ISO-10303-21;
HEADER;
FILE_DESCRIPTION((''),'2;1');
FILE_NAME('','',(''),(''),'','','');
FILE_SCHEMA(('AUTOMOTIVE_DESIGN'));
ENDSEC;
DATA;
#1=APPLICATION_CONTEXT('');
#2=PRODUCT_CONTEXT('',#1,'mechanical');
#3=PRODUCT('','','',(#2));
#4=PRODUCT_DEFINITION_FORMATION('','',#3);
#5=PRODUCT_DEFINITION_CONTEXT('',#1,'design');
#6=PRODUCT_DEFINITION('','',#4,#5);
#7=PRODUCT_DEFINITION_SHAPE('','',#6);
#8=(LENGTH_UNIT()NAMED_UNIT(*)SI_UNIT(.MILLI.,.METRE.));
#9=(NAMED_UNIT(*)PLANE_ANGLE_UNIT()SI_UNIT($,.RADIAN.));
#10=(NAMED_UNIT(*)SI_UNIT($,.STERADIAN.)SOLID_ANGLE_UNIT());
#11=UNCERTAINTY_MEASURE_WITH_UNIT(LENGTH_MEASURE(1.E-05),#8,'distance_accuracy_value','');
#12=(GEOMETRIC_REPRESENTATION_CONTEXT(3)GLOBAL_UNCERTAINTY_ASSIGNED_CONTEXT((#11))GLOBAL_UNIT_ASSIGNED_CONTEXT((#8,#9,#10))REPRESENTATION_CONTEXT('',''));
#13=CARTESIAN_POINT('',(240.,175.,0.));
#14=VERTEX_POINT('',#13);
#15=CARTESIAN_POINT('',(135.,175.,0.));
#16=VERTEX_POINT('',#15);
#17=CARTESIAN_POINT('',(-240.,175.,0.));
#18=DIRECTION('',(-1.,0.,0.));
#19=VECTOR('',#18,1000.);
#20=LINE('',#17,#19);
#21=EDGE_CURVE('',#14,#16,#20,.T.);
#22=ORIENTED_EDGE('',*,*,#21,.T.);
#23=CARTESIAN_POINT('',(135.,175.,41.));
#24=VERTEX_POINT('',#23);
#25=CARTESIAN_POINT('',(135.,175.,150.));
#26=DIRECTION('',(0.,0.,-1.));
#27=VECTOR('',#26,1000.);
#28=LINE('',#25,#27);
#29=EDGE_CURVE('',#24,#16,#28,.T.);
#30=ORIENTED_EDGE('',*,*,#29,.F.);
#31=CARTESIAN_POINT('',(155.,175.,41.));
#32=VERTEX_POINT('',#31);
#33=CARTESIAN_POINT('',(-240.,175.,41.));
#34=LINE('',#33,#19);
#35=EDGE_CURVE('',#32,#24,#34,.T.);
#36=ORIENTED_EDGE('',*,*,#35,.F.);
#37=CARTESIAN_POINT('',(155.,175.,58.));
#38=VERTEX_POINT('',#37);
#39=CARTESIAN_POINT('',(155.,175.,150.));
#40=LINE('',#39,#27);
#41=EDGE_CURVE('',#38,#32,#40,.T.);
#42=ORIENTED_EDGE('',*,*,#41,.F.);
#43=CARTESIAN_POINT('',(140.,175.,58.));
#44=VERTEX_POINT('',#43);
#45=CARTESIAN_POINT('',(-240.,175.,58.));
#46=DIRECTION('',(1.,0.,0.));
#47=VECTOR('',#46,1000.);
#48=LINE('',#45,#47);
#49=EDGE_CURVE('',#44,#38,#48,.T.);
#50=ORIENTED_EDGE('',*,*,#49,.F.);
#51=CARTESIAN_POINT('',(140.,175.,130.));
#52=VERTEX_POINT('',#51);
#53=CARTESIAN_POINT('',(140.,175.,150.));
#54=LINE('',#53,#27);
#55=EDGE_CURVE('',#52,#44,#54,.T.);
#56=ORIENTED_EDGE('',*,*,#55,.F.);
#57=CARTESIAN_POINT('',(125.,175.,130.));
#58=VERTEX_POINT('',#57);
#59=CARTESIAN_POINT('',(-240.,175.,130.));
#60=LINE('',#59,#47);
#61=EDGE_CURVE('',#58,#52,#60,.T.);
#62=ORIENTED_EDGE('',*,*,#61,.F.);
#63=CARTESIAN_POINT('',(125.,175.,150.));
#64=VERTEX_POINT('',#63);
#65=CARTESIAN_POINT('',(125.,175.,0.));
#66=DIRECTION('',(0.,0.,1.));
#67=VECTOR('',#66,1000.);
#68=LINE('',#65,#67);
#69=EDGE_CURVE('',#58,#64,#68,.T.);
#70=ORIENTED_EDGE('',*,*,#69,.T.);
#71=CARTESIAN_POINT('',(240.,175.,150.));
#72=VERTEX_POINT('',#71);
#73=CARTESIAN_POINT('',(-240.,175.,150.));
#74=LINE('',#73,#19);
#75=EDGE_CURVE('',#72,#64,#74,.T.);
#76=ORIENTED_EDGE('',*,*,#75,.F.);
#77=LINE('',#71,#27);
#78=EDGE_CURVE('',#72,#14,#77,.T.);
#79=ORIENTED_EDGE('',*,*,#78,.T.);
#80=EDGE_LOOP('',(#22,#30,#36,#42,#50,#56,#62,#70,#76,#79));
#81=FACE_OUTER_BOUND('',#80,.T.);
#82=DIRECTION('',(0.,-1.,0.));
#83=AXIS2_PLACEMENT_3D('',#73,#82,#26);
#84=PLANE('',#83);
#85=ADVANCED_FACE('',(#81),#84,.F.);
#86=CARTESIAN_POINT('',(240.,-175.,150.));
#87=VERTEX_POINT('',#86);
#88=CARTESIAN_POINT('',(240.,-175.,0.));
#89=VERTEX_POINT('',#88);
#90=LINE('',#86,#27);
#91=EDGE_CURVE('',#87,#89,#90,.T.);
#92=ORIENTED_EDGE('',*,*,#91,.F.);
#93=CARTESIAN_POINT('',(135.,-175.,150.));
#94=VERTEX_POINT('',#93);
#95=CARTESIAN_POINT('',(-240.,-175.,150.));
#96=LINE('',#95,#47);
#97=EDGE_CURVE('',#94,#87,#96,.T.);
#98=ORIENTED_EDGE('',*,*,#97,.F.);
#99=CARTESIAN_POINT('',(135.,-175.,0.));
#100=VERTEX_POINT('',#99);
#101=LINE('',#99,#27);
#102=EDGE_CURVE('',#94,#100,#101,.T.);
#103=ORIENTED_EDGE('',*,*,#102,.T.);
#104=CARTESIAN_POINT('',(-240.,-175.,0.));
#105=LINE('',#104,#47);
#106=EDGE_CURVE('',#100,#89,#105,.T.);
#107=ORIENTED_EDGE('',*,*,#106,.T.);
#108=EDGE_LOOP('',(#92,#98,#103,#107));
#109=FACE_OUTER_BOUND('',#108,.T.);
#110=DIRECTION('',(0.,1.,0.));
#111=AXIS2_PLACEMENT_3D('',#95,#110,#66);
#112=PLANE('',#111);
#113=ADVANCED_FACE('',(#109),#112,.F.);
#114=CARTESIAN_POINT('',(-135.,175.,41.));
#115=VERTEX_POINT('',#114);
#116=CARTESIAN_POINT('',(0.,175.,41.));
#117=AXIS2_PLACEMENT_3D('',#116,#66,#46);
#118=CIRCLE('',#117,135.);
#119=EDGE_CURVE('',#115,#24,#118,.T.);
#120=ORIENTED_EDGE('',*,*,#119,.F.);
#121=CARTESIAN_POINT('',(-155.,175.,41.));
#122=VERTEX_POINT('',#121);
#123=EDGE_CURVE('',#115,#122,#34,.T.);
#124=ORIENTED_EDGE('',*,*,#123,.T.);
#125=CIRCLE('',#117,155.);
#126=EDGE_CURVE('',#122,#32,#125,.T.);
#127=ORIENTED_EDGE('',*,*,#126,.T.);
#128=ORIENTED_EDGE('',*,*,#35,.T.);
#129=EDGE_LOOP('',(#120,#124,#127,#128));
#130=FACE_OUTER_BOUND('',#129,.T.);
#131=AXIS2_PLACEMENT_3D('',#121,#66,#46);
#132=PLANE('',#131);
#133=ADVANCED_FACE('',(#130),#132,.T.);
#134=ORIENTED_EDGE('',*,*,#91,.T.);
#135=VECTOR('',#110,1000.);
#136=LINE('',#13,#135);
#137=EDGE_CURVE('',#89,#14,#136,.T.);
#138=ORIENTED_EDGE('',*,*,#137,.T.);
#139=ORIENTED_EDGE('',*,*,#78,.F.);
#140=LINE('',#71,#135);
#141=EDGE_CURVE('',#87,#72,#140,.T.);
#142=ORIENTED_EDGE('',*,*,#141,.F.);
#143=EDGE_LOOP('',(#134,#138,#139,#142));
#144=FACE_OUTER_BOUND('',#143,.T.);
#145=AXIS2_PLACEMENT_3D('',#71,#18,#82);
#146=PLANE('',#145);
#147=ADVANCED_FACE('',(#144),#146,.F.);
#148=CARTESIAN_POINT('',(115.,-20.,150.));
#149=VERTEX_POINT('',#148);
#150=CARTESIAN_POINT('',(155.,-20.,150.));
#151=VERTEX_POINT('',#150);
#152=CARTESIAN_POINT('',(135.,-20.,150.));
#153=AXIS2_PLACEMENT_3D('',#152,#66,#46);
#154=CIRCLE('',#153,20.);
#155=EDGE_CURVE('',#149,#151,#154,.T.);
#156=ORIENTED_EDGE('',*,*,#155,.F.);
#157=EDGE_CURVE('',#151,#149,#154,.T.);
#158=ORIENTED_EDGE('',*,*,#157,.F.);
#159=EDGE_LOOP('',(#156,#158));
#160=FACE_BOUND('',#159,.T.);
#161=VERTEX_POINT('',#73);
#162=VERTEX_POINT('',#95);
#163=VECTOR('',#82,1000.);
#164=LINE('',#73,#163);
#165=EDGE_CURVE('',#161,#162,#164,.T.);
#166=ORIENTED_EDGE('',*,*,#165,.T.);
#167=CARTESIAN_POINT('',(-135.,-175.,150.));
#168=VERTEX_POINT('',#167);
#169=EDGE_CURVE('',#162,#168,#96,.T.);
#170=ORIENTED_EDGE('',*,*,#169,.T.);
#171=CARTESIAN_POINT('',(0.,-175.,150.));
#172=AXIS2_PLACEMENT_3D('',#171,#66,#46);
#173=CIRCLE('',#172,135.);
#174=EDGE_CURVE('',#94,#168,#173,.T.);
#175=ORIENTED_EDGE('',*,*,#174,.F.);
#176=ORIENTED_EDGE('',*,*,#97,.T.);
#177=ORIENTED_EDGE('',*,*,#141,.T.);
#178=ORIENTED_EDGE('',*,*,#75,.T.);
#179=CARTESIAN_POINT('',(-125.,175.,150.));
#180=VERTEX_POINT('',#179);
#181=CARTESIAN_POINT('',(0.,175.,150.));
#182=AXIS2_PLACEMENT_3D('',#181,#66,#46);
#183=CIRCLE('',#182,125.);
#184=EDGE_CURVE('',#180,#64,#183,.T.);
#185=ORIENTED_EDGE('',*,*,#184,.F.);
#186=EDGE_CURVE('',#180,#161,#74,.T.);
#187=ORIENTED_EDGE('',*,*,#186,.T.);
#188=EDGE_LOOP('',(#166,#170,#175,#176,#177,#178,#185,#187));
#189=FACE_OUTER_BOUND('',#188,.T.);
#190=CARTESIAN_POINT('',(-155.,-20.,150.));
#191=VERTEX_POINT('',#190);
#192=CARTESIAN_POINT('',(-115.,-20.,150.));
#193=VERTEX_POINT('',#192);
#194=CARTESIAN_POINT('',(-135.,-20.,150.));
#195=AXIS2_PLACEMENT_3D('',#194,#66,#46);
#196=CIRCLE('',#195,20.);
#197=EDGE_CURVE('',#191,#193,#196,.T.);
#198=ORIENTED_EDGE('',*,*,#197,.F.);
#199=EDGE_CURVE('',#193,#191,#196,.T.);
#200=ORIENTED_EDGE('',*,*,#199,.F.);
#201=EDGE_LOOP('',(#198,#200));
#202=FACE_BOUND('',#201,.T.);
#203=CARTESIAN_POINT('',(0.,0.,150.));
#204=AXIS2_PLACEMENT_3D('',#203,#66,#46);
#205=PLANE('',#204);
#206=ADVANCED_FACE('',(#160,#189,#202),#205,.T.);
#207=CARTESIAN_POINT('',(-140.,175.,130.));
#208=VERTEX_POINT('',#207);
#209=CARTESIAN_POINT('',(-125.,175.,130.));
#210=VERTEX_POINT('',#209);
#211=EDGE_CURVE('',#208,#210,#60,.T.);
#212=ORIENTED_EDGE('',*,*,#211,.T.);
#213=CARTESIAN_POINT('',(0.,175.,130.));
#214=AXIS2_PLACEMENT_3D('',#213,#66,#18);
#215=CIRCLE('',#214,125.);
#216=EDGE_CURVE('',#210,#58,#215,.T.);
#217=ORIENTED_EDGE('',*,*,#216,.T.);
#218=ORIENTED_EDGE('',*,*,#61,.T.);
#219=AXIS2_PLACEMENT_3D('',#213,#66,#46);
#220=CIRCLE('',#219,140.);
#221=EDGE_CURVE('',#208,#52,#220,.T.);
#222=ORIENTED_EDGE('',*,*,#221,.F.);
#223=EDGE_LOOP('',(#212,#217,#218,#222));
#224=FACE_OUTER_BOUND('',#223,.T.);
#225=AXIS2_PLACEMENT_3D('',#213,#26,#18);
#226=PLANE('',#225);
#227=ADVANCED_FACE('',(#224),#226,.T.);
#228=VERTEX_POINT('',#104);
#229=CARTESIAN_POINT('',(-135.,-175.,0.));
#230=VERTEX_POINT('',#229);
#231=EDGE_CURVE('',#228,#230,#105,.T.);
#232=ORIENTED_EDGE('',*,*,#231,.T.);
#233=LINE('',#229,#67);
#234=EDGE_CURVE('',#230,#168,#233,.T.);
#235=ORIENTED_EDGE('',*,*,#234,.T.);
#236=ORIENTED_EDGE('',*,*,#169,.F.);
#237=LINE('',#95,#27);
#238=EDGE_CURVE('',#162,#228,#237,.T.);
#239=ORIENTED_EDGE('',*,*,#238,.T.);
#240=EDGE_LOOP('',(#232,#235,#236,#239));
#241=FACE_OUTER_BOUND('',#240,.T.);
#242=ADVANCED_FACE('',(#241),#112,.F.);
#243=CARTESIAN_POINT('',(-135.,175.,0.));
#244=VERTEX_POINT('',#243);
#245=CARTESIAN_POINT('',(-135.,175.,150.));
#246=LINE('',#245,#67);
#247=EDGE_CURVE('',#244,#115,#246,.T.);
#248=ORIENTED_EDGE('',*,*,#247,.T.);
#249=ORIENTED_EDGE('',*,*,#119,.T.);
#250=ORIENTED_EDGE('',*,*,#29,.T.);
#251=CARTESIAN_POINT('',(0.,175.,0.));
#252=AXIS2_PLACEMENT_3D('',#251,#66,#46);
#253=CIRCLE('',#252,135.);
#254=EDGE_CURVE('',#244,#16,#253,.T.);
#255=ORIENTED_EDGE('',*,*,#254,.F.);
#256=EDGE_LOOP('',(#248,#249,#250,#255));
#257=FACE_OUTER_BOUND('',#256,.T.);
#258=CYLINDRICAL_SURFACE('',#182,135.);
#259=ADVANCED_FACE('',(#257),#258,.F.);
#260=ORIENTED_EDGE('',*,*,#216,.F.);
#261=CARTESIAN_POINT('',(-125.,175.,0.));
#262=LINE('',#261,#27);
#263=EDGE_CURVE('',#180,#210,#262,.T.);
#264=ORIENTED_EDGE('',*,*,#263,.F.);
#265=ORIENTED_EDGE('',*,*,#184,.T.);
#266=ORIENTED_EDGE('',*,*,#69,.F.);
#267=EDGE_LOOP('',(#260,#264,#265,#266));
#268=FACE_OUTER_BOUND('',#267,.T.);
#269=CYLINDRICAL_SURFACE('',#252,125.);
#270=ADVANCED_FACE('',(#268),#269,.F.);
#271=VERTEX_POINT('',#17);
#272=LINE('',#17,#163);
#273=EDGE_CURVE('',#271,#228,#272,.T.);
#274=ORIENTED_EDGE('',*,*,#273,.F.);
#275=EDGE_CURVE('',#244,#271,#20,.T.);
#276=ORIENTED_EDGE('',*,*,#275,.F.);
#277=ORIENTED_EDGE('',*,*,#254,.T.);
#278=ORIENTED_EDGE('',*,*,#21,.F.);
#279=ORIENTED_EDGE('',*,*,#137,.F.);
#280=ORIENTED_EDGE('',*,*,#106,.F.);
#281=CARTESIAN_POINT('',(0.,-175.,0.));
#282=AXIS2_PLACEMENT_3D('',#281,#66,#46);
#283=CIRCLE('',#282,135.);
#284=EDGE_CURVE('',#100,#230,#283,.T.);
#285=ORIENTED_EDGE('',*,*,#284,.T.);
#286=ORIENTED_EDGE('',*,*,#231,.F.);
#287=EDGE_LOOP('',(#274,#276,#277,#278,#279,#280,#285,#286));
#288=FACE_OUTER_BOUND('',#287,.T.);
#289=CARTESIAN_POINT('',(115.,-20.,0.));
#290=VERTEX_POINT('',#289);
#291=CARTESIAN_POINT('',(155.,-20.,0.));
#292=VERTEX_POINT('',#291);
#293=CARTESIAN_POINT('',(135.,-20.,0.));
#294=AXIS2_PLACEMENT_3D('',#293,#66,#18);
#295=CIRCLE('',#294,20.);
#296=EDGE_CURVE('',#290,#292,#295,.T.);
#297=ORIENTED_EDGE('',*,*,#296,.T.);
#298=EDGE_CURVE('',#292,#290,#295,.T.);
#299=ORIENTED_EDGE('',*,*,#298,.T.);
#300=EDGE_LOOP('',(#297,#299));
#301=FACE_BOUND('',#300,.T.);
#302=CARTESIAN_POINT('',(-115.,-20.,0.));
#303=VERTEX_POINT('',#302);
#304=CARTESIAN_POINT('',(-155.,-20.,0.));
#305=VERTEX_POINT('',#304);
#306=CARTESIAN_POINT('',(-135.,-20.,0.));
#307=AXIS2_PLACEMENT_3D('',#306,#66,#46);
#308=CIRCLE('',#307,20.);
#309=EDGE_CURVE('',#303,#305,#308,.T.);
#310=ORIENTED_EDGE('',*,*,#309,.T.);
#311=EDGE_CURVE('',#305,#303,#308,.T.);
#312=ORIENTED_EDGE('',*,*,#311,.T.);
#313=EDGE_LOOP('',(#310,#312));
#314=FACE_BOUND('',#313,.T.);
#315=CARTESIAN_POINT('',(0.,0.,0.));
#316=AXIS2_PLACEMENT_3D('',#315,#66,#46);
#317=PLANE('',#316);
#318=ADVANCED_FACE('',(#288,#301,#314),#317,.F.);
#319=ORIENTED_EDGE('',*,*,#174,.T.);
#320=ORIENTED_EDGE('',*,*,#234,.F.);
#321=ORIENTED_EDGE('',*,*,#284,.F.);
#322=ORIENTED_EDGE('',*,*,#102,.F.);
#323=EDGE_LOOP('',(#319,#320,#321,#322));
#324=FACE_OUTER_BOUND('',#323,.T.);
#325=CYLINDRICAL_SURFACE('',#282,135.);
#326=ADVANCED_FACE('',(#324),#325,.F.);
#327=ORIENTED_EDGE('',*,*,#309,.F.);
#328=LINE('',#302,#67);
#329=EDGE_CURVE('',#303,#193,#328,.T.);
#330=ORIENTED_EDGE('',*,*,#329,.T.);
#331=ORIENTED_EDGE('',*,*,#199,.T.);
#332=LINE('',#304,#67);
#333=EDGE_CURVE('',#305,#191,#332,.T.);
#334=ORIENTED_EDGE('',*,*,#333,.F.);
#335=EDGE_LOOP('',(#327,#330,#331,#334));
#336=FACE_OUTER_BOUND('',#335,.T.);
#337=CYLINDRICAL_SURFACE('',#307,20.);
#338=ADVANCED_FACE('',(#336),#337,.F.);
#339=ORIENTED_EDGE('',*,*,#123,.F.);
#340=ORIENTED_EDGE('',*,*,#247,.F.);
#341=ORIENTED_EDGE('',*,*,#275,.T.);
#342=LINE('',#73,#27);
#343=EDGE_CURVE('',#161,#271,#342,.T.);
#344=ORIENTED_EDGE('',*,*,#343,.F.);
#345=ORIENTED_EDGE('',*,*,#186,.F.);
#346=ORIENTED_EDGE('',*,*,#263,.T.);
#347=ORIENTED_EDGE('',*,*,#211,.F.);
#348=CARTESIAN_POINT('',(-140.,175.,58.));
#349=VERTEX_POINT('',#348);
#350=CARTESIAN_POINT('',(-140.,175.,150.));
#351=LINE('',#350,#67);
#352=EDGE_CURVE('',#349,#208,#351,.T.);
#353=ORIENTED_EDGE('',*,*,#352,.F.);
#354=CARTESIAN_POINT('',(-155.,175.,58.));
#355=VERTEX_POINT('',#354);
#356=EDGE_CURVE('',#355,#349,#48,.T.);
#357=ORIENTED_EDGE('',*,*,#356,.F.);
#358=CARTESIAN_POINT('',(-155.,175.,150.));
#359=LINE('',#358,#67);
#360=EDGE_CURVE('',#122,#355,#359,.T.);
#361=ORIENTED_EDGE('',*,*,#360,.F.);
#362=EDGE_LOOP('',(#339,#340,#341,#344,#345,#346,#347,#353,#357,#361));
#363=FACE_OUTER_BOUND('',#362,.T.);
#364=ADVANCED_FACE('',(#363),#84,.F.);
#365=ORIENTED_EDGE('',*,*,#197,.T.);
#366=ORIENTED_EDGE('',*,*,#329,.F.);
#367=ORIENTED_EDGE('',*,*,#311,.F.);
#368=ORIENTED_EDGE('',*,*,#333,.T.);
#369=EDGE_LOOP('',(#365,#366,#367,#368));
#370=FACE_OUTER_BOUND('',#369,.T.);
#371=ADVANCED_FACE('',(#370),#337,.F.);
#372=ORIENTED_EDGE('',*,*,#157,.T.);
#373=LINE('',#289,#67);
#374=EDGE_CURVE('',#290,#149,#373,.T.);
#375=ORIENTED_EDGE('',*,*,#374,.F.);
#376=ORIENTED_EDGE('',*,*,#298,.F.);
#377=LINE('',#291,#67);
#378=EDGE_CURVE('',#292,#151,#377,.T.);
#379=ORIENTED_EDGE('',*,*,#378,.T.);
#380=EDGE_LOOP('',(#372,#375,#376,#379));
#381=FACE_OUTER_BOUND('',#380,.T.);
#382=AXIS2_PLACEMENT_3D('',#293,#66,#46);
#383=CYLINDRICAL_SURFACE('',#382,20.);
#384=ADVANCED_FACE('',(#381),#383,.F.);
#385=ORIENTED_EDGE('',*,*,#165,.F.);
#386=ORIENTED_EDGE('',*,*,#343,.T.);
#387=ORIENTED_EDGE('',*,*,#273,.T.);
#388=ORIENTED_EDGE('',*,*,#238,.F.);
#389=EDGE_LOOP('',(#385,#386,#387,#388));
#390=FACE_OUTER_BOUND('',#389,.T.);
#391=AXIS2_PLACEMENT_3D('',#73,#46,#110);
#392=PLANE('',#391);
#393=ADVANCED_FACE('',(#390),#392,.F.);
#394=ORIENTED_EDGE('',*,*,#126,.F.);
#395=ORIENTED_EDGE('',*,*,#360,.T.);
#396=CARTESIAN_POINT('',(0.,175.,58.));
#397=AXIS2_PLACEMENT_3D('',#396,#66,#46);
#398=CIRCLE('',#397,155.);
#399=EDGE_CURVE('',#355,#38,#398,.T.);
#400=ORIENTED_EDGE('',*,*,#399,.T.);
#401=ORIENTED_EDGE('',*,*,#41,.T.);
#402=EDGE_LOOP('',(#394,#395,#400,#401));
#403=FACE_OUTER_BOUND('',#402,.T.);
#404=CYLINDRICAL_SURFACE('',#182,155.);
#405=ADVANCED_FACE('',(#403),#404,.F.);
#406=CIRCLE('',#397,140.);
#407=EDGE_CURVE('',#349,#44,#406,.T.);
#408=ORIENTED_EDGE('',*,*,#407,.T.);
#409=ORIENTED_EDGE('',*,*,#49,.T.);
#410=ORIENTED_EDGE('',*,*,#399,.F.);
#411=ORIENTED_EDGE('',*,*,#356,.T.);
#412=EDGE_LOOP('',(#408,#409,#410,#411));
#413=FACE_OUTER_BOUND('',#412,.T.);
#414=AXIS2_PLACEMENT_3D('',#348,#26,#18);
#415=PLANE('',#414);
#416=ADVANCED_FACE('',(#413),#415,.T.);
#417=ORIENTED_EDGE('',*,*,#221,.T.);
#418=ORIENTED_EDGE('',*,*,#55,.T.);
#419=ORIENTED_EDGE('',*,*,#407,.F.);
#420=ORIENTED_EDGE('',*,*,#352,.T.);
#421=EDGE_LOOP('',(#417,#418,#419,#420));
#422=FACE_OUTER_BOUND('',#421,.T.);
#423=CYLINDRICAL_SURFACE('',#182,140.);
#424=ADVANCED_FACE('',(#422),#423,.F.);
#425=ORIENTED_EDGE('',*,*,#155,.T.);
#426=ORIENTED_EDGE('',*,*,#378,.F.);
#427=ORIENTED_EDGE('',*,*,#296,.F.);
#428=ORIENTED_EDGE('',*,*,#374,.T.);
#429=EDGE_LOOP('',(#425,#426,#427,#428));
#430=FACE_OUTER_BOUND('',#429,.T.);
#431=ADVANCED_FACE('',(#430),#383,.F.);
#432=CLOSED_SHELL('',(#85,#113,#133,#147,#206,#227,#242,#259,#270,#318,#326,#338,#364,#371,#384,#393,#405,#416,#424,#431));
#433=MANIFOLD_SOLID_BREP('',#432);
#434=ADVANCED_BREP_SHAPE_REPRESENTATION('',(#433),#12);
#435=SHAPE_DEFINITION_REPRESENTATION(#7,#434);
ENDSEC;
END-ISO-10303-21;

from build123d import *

# Parameters (mm, degrees)
SKETCH_1_W               = 480
SKETCH_1_H               = 350
EXTRUDE_1_DEPTH          = 150
CUT_EXTRUDE_1_DEPTH      = 333.753662639
CUT_EXTRUDE_1_DEPTH_BACK = 333.753662639
SKETCH_2_R               = 20
CUT_EXTRUDE_2_DEPTH      = 333.753662639
CUT_EXTRUDE_2_DEPTH_BACK = 333.753662639
SKETCH_3_R               = 135
SKETCH_3_R_2             = 125


with BuildPart() as part:
    # 草图1 → 凸台-拉伸1 (new body)
    with BuildSketch(Plane.XY):
        Rectangle(SKETCH_1_W, SKETCH_1_H)
    extrude(amount=EXTRUDE_1_DEPTH)

    # 草图2 → 切除-拉伸1 (cut, two sides: drawn at the far end of the back side and taken through both)
    with BuildSketch(Plane.XY.offset(150).offset(-CUT_EXTRUDE_1_DEPTH_BACK)):
        with Locations((-135, -20)):
            Circle(SKETCH_2_R)
        with Locations((135, -20)):
            Circle(SKETCH_2_R)
    extrude(amount=CUT_EXTRUDE_1_DEPTH + CUT_EXTRUDE_1_DEPTH_BACK, mode=Mode.SUBTRACT)

    # 草图3 → 切除-拉伸2 (cut, two sides: drawn at the far end of the back side and taken through both)
    with BuildSketch(Plane.XY.offset(150).offset(-CUT_EXTRUDE_2_DEPTH_BACK)):
        with Locations((0, -175)):
            Circle(SKETCH_3_R)
        with Locations((0, 175)):
            Circle(SKETCH_3_R_2)
    extrude(amount=CUT_EXTRUDE_2_DEPTH + CUT_EXTRUDE_2_DEPTH_BACK, mode=Mode.SUBTRACT)

    # 草图5 → 切除-旋转1 (revolve, cut)
    with BuildSketch(Plane(origin=(0, 175, 0), x_dir=(1, 0, 0), z_dir=(0, 1, 0))):
        Polygon((0, -130), (-140, -130), (-140, -58), (-155, -58), (-155, -41), (-135, -41), (-135, 0), (0, 0), (0, -41), align=None)
    revolve(axis=Axis((0, 175, 150), (0, 0, -1)), mode=Mode.SUBTRACT)


solid = part.part
